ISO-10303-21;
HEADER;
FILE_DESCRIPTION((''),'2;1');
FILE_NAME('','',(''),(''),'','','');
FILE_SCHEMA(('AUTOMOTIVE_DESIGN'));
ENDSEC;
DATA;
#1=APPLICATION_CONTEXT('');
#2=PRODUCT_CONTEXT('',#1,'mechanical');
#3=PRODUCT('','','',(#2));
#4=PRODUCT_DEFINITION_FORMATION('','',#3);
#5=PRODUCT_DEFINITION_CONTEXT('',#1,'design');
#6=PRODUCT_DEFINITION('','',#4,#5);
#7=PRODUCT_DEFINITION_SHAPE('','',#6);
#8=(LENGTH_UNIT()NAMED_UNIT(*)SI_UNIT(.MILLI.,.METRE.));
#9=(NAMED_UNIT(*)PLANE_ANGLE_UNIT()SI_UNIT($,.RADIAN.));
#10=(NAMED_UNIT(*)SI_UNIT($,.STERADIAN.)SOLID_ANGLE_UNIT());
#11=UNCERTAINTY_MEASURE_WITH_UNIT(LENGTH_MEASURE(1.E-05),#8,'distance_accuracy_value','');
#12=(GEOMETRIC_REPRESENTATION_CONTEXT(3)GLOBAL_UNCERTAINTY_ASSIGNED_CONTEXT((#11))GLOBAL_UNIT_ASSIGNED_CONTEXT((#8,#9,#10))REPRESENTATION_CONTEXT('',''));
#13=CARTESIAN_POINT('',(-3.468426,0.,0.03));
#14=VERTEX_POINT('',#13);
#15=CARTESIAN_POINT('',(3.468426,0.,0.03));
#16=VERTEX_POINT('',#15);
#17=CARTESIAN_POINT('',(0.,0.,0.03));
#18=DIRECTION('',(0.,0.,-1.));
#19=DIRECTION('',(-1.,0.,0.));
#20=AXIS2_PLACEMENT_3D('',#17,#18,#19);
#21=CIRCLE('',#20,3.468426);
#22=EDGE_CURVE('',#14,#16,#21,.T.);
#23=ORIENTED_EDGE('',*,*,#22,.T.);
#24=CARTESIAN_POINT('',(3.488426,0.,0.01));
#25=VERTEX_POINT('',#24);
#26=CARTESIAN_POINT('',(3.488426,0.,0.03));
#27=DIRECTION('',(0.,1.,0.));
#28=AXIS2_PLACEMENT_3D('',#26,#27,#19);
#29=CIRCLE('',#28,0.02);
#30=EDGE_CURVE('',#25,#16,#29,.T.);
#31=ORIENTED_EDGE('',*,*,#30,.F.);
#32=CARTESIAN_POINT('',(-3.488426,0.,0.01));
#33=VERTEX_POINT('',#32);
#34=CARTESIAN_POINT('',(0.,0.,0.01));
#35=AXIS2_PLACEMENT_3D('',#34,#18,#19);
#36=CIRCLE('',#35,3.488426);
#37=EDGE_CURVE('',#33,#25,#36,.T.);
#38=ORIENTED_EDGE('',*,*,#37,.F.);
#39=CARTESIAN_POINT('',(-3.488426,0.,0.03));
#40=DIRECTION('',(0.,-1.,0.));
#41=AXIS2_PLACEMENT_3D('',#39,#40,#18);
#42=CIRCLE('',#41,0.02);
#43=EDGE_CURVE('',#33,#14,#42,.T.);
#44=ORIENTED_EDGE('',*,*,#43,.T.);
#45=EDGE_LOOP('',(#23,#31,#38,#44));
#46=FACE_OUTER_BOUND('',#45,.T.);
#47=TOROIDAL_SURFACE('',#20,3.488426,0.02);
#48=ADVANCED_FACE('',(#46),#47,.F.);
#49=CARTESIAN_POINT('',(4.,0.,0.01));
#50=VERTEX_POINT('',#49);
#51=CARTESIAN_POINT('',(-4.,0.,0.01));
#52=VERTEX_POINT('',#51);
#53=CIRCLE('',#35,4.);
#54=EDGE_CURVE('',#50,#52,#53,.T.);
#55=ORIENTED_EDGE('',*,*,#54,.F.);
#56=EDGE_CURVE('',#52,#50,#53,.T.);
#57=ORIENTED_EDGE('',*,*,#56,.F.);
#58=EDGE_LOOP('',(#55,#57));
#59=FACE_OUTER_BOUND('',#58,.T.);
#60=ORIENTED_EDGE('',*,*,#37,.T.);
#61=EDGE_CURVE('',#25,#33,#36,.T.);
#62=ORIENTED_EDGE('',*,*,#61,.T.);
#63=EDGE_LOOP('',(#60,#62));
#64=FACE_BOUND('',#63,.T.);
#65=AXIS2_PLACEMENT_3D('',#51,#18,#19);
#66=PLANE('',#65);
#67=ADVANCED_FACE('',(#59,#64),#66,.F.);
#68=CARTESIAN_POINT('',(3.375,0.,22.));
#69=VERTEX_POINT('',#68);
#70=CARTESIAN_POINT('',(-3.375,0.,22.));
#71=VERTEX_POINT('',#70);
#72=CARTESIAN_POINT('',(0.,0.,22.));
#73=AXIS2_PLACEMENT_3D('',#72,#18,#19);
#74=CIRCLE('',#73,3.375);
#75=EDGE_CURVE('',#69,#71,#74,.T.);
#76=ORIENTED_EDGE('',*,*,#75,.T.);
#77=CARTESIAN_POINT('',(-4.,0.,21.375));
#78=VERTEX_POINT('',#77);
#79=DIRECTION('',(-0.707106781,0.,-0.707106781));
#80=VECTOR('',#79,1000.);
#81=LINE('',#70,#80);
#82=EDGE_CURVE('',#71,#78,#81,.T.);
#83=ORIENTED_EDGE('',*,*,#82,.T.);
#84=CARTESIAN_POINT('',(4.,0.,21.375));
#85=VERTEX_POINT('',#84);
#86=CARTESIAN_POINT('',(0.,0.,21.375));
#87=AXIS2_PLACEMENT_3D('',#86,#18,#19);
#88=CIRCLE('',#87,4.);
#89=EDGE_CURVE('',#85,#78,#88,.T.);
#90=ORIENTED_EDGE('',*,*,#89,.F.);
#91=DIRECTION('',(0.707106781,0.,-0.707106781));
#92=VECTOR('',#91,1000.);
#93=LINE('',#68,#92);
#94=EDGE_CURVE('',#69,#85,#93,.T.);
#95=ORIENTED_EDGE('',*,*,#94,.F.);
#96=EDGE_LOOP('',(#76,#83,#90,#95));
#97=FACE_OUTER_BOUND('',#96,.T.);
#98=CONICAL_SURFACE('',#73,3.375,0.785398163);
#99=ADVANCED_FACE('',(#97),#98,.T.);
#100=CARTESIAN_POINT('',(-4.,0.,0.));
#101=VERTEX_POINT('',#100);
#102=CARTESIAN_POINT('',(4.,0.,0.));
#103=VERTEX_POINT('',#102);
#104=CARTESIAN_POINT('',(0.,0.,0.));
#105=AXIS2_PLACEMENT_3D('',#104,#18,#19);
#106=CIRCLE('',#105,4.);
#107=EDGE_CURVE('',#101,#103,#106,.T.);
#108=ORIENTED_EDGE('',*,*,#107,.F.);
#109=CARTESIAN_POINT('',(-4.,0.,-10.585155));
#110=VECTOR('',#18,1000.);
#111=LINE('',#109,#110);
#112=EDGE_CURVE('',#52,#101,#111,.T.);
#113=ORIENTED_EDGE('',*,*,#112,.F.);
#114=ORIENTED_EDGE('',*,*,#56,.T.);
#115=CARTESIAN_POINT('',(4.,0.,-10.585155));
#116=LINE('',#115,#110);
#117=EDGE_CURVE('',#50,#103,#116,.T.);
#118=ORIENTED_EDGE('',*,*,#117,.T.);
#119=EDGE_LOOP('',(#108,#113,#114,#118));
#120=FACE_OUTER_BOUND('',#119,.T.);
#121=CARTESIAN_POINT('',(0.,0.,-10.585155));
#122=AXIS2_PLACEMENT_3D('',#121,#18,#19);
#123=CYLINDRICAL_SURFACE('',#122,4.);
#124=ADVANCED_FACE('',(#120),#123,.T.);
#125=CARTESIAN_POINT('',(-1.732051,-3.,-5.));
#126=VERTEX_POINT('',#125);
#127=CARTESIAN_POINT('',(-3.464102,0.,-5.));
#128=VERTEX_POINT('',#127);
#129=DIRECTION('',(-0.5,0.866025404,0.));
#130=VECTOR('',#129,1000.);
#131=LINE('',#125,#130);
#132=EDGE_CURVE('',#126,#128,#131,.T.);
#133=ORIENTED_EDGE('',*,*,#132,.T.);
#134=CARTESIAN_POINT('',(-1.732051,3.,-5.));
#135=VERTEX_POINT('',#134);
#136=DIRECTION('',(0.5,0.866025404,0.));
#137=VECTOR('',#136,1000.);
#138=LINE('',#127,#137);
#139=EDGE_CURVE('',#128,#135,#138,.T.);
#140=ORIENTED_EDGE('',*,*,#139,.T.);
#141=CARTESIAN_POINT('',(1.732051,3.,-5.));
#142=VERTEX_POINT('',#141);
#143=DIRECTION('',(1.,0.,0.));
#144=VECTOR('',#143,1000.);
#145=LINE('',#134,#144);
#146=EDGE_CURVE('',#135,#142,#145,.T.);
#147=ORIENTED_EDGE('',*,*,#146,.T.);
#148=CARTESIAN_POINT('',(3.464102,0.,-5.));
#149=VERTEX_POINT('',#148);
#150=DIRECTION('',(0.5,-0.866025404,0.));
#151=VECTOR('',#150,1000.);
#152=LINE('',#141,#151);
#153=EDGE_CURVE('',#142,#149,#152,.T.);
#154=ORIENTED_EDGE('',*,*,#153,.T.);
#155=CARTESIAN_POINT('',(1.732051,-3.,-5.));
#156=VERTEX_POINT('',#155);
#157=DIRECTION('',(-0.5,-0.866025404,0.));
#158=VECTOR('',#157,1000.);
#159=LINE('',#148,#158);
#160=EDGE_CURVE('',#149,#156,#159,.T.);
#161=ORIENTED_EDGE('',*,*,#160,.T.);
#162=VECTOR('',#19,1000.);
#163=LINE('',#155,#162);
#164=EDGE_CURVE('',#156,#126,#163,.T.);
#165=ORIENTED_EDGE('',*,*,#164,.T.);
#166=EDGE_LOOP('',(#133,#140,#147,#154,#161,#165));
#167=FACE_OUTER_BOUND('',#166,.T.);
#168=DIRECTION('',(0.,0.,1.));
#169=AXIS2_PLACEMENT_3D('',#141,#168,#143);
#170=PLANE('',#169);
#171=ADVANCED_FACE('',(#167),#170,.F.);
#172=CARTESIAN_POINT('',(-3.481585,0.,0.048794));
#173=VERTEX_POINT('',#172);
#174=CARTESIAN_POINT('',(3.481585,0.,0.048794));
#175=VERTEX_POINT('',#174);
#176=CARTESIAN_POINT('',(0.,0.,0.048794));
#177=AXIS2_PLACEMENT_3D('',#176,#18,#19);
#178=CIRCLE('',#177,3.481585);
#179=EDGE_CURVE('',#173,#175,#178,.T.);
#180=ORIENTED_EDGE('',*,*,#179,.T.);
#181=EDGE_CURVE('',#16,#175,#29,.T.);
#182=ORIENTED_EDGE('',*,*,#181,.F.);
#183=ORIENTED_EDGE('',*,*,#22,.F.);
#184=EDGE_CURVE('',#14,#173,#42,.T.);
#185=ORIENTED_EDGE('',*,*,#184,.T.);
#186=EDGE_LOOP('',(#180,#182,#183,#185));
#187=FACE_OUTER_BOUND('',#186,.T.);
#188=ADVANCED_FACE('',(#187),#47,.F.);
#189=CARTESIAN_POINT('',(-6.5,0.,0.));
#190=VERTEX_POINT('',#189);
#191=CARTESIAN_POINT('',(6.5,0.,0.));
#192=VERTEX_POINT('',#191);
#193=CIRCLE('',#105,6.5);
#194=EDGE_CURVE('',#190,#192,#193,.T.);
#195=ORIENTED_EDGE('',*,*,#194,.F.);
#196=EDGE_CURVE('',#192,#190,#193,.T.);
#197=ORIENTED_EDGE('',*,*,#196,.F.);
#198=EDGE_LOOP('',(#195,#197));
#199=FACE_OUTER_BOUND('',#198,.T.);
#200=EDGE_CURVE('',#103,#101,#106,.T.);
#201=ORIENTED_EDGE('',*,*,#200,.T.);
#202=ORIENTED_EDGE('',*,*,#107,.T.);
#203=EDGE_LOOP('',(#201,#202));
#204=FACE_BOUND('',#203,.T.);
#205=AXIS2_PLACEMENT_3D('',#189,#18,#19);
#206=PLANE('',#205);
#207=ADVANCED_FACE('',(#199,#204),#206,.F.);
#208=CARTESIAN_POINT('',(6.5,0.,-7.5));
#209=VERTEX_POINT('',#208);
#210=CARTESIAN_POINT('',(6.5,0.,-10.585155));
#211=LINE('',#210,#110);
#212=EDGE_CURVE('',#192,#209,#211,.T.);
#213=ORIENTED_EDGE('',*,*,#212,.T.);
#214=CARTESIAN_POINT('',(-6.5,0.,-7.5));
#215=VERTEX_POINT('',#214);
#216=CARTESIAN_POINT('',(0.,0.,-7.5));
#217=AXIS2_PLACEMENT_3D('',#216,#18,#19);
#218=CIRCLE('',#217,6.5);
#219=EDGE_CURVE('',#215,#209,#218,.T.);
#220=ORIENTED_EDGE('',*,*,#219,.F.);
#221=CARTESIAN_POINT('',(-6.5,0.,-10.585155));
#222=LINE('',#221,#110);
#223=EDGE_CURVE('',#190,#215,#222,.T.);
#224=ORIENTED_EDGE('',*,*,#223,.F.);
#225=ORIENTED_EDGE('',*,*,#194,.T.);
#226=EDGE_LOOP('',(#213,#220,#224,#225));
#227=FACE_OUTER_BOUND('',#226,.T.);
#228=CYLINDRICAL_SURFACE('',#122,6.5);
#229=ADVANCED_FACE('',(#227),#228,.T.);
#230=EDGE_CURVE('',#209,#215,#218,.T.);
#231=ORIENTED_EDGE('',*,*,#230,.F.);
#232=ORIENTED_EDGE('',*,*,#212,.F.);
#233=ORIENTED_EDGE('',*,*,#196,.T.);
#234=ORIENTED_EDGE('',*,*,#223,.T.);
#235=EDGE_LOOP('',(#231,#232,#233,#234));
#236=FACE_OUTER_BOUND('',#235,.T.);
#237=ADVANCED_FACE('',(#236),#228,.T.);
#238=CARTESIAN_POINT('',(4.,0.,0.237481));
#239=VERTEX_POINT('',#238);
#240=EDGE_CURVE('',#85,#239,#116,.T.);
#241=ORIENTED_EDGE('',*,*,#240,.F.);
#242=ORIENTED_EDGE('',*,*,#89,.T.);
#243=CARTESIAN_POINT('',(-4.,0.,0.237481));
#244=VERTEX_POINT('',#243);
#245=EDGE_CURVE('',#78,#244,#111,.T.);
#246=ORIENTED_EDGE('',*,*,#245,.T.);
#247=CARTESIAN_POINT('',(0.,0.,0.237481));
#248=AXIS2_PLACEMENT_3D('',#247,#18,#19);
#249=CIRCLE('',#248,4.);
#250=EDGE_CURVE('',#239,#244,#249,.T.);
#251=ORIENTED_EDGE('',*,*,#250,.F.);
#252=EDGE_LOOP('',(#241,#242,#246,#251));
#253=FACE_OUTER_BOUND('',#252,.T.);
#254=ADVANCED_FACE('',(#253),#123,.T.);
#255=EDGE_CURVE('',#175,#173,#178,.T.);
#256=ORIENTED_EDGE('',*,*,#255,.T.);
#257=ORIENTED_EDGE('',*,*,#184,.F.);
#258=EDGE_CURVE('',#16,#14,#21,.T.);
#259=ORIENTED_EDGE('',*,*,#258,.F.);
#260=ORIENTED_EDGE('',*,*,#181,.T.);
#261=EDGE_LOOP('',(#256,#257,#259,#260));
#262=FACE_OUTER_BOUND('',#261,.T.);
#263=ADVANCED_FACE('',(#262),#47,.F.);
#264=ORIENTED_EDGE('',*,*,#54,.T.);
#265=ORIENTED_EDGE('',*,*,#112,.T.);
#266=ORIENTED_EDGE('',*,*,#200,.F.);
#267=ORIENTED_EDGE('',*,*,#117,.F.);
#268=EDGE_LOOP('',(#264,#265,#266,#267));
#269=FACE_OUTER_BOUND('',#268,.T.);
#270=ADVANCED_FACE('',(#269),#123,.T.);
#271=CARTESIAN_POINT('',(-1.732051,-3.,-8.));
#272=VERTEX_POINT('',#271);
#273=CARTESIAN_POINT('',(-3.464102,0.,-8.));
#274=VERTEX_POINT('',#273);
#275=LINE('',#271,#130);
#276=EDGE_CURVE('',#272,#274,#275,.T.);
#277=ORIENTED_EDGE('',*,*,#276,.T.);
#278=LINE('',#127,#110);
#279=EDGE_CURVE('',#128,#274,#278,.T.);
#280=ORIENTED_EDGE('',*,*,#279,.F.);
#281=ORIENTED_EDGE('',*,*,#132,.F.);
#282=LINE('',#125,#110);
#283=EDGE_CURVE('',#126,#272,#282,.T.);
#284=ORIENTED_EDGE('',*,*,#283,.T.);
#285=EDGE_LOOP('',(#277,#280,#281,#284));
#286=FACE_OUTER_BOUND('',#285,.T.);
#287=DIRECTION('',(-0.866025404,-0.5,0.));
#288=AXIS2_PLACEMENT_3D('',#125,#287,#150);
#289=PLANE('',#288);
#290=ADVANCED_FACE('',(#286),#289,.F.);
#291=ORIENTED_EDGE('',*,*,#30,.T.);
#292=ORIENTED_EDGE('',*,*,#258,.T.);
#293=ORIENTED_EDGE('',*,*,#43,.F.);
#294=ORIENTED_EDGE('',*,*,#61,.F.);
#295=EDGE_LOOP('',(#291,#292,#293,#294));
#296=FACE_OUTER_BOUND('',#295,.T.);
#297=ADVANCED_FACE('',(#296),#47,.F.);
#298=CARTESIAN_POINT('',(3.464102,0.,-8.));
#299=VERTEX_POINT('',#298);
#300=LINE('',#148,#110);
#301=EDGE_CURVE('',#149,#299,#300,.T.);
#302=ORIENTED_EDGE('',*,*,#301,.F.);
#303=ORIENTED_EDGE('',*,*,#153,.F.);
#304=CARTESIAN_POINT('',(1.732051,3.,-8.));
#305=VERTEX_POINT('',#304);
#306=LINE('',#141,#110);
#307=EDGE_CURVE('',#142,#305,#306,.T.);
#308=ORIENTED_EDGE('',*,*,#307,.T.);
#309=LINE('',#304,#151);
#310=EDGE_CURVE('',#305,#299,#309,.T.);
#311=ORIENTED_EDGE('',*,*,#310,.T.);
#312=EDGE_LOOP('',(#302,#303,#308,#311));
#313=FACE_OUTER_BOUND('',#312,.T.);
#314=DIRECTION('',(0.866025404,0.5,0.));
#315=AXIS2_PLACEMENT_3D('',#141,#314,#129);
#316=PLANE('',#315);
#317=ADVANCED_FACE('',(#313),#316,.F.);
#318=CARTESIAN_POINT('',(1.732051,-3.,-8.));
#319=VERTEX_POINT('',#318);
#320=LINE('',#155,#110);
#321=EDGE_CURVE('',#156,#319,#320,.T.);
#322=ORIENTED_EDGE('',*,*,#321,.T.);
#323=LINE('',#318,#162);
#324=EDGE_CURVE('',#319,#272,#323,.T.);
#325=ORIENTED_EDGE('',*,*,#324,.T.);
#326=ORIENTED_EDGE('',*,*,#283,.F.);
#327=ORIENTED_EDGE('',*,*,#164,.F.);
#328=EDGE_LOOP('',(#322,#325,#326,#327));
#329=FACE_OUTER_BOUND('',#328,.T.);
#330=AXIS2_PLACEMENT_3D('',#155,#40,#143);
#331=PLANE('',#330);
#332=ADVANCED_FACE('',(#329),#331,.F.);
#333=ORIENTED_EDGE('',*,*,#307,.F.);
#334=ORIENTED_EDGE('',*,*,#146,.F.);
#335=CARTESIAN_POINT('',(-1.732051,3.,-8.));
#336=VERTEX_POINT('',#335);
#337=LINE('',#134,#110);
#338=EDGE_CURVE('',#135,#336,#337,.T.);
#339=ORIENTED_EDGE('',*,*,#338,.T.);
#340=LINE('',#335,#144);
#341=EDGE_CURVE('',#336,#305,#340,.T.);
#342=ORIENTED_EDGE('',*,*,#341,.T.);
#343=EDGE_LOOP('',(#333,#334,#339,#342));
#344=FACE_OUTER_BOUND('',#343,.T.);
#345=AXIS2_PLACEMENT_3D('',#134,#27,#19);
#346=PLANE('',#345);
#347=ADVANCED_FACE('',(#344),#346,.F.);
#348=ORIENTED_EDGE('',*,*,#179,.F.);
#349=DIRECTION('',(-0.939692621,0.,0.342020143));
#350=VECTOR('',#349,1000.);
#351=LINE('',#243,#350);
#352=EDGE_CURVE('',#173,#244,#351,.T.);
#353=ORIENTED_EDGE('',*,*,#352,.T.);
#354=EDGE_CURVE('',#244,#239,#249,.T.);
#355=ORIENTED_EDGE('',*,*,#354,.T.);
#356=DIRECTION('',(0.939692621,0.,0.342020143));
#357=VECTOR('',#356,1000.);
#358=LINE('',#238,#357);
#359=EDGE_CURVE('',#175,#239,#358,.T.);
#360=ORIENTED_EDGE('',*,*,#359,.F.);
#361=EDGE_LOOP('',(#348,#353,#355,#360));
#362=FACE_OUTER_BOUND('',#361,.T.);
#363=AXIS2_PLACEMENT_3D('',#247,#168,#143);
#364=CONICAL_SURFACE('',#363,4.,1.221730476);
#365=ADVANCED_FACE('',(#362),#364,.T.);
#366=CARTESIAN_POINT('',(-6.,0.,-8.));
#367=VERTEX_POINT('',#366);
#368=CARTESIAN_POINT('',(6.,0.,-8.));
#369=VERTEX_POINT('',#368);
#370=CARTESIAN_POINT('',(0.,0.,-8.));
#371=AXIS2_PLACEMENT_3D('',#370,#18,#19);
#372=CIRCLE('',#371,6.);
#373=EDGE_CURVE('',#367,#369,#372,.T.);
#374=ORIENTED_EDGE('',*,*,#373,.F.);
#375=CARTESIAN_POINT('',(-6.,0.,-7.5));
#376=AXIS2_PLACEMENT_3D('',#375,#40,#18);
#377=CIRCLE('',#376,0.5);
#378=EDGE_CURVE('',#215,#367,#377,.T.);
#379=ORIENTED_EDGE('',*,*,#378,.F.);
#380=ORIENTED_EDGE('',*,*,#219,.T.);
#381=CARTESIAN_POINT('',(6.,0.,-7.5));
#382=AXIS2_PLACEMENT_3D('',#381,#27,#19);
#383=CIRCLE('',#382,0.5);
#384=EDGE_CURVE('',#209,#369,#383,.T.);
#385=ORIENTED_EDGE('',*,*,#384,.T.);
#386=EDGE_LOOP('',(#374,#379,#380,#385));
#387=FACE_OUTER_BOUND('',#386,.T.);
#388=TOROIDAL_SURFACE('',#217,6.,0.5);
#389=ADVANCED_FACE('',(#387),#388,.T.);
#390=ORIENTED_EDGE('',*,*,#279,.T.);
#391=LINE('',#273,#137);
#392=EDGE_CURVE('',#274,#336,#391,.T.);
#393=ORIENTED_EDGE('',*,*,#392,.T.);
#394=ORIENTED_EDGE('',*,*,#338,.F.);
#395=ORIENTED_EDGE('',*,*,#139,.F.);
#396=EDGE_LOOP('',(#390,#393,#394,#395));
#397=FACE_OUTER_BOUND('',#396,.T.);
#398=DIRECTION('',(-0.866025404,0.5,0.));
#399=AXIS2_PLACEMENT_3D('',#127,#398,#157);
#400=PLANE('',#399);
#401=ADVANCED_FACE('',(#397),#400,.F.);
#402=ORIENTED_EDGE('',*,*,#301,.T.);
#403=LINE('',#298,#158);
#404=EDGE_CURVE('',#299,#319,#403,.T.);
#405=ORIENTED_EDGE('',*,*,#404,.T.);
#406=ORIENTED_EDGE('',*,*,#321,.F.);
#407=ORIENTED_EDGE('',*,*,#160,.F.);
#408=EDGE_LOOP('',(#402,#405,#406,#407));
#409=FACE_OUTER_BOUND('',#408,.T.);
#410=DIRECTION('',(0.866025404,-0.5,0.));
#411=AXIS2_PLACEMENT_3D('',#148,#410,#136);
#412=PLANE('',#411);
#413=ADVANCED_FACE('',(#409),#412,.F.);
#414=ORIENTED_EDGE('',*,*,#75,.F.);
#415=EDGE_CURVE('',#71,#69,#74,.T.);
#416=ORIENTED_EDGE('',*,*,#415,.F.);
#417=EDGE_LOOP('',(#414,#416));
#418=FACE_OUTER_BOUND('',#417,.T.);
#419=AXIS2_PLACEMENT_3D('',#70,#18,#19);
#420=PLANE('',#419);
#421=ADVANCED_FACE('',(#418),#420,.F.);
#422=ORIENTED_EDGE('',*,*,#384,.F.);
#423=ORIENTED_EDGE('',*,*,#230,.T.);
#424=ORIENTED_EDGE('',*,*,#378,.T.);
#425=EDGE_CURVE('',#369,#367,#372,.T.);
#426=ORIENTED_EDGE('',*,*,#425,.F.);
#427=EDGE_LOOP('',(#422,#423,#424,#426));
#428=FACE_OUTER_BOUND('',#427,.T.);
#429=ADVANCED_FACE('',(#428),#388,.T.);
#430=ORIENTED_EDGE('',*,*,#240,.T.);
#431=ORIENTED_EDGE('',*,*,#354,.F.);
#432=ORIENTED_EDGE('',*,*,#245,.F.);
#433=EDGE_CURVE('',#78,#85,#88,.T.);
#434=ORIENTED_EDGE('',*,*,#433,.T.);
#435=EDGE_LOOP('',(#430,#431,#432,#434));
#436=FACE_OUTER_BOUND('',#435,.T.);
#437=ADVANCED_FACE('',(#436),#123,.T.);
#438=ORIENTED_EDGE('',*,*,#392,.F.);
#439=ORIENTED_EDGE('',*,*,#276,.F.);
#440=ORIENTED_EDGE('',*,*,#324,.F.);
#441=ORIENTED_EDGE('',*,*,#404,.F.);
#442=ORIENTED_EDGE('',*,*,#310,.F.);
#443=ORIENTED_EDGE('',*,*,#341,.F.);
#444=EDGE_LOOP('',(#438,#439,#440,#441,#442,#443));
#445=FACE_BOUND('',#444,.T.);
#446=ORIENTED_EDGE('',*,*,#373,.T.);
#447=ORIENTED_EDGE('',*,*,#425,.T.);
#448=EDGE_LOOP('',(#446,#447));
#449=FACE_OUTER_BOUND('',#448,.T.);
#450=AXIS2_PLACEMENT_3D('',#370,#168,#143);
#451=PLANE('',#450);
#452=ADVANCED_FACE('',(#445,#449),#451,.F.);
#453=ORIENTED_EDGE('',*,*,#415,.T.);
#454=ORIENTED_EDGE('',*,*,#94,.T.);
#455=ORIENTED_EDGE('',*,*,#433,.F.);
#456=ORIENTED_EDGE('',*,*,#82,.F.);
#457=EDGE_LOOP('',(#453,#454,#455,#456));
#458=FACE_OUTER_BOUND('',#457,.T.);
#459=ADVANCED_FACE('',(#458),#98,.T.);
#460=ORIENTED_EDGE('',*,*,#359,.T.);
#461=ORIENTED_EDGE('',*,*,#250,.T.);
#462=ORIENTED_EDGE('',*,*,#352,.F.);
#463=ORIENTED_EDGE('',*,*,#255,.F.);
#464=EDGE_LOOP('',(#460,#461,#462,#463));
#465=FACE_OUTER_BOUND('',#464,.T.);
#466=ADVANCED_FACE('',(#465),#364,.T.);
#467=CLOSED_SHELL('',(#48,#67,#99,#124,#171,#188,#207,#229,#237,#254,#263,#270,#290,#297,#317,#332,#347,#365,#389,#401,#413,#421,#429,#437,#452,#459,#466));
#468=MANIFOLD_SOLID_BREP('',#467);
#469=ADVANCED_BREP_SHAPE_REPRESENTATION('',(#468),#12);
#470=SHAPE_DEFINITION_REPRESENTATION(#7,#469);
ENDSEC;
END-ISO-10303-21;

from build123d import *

# Parameters (mm, degrees)
CUT_EXTRUDE1_DEPTH = 3


with BuildPart() as part:
    # Logo3_bib1 → Revolve1 (revolve)
    with BuildSketch(Plane(origin=(0, 0, 0), x_dir=(-1, 0, 0), z_dir=(0, -1, 0))):
        with BuildLine():
            Line((0, -22), (0, 8))
            Line((0, 8), (6, 8))
            ThreePointArc((6, 8), (6.353553391, 7.853553391), (6.5, 7.5))
            Line((6.5, 7.5), (6.5, 0))
            Line((6.5, 0), (4, 0))
            Line((4, 0), (4, -0.01))
            Line((4, -0.01), (3.488425636, -0.01))
            ThreePointArc((3.488425636, -0.01), (3.468729481, -0.026527036), (3.481585234, -0.048793852))
            Line((3.481585234, -0.048793852), (4, -0.237481396))
            Line((4, -0.237481396), (4, -21.375))
            Line((4, -21.375), (3.375, -22))
            Line((3.375, -22), (0, -22))
        make_face()
    revolve(axis=Axis((0, 0, -10.585154653), (0, 0, 1)))

    # Logo3_bib2 → Cut-Extrude1 (cut)
    with BuildSketch(Plane(origin=(0, 0, -8), x_dir=(1, 0, 0), z_dir=(0, 0, -1))):
        Polygon((3.464101615, 0), (1.732050808, 3), (-1.732050808, 3), (-3.464101615, 0), (-1.732050808, -3), (1.732050808, -3), align=None)
    extrude(amount=-CUT_EXTRUDE1_DEPTH, mode=Mode.SUBTRACT)


solid = part.part
